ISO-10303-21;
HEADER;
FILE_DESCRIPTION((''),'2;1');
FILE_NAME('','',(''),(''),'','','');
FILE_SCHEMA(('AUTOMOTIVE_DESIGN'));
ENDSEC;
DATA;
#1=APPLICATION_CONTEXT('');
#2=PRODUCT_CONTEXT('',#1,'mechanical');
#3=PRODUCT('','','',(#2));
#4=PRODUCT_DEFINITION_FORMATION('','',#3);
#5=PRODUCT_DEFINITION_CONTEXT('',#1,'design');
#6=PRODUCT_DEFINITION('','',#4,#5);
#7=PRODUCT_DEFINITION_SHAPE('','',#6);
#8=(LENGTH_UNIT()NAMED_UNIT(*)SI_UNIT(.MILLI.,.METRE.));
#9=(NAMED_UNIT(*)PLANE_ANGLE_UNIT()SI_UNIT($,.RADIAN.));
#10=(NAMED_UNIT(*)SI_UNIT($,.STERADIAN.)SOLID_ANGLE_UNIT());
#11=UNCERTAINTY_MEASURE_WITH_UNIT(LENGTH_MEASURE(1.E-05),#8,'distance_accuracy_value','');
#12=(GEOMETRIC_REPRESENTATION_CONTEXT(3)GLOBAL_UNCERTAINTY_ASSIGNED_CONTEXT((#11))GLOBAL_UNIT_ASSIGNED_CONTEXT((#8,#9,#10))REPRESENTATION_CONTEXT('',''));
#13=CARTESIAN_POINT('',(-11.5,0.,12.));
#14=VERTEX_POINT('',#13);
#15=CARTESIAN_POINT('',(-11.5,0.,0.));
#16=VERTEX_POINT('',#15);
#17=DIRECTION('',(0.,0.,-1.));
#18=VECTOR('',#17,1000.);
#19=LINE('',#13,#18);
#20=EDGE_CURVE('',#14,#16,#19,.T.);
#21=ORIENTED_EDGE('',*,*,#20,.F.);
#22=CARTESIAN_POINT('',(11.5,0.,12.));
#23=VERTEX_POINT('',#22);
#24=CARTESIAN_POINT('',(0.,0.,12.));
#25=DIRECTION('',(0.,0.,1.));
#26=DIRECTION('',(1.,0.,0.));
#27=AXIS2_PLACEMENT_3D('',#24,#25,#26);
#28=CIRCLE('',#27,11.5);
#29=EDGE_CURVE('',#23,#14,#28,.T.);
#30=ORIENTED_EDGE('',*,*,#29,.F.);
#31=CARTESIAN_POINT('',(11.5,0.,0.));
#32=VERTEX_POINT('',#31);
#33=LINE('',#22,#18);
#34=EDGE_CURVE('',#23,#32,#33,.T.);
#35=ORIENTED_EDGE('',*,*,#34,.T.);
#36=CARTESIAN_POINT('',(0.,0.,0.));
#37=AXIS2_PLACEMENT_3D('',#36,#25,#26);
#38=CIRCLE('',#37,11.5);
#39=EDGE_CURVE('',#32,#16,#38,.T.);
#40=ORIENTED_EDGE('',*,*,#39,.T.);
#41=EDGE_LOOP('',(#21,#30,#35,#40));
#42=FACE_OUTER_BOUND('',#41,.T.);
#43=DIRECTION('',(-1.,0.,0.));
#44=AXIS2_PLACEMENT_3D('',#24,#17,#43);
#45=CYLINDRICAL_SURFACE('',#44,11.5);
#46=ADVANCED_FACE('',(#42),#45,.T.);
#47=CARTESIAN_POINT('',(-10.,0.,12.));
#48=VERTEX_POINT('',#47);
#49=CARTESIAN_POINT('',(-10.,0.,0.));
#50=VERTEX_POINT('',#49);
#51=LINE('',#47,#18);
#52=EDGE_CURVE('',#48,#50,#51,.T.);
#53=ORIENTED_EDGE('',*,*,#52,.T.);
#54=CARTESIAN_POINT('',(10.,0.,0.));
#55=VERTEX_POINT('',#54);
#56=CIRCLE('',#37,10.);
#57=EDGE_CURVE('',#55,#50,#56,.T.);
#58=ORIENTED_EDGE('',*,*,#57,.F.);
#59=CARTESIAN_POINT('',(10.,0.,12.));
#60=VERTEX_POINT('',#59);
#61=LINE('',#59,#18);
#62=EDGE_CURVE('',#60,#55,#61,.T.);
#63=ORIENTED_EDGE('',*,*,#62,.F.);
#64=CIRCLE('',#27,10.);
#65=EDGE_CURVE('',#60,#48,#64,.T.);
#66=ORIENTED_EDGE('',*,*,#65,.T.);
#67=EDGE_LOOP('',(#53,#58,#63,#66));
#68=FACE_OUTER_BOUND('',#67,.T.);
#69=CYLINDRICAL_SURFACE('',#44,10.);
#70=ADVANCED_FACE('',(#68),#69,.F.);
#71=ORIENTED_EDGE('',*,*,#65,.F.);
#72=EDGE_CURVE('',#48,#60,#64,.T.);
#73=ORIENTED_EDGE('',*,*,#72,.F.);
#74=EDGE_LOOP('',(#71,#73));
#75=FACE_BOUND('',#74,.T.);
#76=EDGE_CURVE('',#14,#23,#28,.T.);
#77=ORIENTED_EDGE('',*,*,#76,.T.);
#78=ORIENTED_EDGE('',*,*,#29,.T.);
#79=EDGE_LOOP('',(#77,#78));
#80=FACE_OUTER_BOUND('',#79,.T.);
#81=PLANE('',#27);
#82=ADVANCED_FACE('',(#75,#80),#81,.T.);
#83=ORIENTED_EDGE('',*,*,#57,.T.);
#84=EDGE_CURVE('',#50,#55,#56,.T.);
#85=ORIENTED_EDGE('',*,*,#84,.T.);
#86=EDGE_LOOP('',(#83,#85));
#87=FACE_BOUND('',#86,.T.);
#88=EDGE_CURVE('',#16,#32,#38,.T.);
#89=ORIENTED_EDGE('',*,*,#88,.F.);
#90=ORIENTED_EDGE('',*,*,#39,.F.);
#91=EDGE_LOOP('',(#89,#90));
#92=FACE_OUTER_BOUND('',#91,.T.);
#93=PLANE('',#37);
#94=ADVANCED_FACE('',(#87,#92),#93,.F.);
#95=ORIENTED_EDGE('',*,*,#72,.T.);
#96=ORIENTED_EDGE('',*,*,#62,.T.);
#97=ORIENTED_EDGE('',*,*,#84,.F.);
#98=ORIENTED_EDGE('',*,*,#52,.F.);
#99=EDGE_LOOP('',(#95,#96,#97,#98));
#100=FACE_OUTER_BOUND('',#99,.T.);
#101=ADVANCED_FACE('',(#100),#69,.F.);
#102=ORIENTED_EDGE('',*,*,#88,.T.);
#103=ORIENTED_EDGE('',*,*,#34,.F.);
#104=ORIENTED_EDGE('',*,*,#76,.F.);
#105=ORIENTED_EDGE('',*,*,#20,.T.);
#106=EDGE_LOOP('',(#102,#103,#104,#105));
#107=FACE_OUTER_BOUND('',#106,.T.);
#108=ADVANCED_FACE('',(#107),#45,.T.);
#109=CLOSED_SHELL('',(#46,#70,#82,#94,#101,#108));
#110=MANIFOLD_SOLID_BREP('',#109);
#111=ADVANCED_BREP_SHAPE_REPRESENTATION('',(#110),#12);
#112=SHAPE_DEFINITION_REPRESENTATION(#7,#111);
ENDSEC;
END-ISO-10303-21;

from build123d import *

# Parameters (mm, degrees)
SKETCH1_R           = 11.5
SKETCH1_R_2         = 10
BOSS_EXTRUDE1_DEPTH = 12


with BuildPart() as part:
    # Sketch1 → Boss-Extrude1 (new body)
    with BuildSketch(Plane.XY):
        Circle(SKETCH1_R)
        Circle(SKETCH1_R_2, mode=Mode.SUBTRACT)
    extrude(amount=BOSS_EXTRUDE1_DEPTH)


solid = part.part
